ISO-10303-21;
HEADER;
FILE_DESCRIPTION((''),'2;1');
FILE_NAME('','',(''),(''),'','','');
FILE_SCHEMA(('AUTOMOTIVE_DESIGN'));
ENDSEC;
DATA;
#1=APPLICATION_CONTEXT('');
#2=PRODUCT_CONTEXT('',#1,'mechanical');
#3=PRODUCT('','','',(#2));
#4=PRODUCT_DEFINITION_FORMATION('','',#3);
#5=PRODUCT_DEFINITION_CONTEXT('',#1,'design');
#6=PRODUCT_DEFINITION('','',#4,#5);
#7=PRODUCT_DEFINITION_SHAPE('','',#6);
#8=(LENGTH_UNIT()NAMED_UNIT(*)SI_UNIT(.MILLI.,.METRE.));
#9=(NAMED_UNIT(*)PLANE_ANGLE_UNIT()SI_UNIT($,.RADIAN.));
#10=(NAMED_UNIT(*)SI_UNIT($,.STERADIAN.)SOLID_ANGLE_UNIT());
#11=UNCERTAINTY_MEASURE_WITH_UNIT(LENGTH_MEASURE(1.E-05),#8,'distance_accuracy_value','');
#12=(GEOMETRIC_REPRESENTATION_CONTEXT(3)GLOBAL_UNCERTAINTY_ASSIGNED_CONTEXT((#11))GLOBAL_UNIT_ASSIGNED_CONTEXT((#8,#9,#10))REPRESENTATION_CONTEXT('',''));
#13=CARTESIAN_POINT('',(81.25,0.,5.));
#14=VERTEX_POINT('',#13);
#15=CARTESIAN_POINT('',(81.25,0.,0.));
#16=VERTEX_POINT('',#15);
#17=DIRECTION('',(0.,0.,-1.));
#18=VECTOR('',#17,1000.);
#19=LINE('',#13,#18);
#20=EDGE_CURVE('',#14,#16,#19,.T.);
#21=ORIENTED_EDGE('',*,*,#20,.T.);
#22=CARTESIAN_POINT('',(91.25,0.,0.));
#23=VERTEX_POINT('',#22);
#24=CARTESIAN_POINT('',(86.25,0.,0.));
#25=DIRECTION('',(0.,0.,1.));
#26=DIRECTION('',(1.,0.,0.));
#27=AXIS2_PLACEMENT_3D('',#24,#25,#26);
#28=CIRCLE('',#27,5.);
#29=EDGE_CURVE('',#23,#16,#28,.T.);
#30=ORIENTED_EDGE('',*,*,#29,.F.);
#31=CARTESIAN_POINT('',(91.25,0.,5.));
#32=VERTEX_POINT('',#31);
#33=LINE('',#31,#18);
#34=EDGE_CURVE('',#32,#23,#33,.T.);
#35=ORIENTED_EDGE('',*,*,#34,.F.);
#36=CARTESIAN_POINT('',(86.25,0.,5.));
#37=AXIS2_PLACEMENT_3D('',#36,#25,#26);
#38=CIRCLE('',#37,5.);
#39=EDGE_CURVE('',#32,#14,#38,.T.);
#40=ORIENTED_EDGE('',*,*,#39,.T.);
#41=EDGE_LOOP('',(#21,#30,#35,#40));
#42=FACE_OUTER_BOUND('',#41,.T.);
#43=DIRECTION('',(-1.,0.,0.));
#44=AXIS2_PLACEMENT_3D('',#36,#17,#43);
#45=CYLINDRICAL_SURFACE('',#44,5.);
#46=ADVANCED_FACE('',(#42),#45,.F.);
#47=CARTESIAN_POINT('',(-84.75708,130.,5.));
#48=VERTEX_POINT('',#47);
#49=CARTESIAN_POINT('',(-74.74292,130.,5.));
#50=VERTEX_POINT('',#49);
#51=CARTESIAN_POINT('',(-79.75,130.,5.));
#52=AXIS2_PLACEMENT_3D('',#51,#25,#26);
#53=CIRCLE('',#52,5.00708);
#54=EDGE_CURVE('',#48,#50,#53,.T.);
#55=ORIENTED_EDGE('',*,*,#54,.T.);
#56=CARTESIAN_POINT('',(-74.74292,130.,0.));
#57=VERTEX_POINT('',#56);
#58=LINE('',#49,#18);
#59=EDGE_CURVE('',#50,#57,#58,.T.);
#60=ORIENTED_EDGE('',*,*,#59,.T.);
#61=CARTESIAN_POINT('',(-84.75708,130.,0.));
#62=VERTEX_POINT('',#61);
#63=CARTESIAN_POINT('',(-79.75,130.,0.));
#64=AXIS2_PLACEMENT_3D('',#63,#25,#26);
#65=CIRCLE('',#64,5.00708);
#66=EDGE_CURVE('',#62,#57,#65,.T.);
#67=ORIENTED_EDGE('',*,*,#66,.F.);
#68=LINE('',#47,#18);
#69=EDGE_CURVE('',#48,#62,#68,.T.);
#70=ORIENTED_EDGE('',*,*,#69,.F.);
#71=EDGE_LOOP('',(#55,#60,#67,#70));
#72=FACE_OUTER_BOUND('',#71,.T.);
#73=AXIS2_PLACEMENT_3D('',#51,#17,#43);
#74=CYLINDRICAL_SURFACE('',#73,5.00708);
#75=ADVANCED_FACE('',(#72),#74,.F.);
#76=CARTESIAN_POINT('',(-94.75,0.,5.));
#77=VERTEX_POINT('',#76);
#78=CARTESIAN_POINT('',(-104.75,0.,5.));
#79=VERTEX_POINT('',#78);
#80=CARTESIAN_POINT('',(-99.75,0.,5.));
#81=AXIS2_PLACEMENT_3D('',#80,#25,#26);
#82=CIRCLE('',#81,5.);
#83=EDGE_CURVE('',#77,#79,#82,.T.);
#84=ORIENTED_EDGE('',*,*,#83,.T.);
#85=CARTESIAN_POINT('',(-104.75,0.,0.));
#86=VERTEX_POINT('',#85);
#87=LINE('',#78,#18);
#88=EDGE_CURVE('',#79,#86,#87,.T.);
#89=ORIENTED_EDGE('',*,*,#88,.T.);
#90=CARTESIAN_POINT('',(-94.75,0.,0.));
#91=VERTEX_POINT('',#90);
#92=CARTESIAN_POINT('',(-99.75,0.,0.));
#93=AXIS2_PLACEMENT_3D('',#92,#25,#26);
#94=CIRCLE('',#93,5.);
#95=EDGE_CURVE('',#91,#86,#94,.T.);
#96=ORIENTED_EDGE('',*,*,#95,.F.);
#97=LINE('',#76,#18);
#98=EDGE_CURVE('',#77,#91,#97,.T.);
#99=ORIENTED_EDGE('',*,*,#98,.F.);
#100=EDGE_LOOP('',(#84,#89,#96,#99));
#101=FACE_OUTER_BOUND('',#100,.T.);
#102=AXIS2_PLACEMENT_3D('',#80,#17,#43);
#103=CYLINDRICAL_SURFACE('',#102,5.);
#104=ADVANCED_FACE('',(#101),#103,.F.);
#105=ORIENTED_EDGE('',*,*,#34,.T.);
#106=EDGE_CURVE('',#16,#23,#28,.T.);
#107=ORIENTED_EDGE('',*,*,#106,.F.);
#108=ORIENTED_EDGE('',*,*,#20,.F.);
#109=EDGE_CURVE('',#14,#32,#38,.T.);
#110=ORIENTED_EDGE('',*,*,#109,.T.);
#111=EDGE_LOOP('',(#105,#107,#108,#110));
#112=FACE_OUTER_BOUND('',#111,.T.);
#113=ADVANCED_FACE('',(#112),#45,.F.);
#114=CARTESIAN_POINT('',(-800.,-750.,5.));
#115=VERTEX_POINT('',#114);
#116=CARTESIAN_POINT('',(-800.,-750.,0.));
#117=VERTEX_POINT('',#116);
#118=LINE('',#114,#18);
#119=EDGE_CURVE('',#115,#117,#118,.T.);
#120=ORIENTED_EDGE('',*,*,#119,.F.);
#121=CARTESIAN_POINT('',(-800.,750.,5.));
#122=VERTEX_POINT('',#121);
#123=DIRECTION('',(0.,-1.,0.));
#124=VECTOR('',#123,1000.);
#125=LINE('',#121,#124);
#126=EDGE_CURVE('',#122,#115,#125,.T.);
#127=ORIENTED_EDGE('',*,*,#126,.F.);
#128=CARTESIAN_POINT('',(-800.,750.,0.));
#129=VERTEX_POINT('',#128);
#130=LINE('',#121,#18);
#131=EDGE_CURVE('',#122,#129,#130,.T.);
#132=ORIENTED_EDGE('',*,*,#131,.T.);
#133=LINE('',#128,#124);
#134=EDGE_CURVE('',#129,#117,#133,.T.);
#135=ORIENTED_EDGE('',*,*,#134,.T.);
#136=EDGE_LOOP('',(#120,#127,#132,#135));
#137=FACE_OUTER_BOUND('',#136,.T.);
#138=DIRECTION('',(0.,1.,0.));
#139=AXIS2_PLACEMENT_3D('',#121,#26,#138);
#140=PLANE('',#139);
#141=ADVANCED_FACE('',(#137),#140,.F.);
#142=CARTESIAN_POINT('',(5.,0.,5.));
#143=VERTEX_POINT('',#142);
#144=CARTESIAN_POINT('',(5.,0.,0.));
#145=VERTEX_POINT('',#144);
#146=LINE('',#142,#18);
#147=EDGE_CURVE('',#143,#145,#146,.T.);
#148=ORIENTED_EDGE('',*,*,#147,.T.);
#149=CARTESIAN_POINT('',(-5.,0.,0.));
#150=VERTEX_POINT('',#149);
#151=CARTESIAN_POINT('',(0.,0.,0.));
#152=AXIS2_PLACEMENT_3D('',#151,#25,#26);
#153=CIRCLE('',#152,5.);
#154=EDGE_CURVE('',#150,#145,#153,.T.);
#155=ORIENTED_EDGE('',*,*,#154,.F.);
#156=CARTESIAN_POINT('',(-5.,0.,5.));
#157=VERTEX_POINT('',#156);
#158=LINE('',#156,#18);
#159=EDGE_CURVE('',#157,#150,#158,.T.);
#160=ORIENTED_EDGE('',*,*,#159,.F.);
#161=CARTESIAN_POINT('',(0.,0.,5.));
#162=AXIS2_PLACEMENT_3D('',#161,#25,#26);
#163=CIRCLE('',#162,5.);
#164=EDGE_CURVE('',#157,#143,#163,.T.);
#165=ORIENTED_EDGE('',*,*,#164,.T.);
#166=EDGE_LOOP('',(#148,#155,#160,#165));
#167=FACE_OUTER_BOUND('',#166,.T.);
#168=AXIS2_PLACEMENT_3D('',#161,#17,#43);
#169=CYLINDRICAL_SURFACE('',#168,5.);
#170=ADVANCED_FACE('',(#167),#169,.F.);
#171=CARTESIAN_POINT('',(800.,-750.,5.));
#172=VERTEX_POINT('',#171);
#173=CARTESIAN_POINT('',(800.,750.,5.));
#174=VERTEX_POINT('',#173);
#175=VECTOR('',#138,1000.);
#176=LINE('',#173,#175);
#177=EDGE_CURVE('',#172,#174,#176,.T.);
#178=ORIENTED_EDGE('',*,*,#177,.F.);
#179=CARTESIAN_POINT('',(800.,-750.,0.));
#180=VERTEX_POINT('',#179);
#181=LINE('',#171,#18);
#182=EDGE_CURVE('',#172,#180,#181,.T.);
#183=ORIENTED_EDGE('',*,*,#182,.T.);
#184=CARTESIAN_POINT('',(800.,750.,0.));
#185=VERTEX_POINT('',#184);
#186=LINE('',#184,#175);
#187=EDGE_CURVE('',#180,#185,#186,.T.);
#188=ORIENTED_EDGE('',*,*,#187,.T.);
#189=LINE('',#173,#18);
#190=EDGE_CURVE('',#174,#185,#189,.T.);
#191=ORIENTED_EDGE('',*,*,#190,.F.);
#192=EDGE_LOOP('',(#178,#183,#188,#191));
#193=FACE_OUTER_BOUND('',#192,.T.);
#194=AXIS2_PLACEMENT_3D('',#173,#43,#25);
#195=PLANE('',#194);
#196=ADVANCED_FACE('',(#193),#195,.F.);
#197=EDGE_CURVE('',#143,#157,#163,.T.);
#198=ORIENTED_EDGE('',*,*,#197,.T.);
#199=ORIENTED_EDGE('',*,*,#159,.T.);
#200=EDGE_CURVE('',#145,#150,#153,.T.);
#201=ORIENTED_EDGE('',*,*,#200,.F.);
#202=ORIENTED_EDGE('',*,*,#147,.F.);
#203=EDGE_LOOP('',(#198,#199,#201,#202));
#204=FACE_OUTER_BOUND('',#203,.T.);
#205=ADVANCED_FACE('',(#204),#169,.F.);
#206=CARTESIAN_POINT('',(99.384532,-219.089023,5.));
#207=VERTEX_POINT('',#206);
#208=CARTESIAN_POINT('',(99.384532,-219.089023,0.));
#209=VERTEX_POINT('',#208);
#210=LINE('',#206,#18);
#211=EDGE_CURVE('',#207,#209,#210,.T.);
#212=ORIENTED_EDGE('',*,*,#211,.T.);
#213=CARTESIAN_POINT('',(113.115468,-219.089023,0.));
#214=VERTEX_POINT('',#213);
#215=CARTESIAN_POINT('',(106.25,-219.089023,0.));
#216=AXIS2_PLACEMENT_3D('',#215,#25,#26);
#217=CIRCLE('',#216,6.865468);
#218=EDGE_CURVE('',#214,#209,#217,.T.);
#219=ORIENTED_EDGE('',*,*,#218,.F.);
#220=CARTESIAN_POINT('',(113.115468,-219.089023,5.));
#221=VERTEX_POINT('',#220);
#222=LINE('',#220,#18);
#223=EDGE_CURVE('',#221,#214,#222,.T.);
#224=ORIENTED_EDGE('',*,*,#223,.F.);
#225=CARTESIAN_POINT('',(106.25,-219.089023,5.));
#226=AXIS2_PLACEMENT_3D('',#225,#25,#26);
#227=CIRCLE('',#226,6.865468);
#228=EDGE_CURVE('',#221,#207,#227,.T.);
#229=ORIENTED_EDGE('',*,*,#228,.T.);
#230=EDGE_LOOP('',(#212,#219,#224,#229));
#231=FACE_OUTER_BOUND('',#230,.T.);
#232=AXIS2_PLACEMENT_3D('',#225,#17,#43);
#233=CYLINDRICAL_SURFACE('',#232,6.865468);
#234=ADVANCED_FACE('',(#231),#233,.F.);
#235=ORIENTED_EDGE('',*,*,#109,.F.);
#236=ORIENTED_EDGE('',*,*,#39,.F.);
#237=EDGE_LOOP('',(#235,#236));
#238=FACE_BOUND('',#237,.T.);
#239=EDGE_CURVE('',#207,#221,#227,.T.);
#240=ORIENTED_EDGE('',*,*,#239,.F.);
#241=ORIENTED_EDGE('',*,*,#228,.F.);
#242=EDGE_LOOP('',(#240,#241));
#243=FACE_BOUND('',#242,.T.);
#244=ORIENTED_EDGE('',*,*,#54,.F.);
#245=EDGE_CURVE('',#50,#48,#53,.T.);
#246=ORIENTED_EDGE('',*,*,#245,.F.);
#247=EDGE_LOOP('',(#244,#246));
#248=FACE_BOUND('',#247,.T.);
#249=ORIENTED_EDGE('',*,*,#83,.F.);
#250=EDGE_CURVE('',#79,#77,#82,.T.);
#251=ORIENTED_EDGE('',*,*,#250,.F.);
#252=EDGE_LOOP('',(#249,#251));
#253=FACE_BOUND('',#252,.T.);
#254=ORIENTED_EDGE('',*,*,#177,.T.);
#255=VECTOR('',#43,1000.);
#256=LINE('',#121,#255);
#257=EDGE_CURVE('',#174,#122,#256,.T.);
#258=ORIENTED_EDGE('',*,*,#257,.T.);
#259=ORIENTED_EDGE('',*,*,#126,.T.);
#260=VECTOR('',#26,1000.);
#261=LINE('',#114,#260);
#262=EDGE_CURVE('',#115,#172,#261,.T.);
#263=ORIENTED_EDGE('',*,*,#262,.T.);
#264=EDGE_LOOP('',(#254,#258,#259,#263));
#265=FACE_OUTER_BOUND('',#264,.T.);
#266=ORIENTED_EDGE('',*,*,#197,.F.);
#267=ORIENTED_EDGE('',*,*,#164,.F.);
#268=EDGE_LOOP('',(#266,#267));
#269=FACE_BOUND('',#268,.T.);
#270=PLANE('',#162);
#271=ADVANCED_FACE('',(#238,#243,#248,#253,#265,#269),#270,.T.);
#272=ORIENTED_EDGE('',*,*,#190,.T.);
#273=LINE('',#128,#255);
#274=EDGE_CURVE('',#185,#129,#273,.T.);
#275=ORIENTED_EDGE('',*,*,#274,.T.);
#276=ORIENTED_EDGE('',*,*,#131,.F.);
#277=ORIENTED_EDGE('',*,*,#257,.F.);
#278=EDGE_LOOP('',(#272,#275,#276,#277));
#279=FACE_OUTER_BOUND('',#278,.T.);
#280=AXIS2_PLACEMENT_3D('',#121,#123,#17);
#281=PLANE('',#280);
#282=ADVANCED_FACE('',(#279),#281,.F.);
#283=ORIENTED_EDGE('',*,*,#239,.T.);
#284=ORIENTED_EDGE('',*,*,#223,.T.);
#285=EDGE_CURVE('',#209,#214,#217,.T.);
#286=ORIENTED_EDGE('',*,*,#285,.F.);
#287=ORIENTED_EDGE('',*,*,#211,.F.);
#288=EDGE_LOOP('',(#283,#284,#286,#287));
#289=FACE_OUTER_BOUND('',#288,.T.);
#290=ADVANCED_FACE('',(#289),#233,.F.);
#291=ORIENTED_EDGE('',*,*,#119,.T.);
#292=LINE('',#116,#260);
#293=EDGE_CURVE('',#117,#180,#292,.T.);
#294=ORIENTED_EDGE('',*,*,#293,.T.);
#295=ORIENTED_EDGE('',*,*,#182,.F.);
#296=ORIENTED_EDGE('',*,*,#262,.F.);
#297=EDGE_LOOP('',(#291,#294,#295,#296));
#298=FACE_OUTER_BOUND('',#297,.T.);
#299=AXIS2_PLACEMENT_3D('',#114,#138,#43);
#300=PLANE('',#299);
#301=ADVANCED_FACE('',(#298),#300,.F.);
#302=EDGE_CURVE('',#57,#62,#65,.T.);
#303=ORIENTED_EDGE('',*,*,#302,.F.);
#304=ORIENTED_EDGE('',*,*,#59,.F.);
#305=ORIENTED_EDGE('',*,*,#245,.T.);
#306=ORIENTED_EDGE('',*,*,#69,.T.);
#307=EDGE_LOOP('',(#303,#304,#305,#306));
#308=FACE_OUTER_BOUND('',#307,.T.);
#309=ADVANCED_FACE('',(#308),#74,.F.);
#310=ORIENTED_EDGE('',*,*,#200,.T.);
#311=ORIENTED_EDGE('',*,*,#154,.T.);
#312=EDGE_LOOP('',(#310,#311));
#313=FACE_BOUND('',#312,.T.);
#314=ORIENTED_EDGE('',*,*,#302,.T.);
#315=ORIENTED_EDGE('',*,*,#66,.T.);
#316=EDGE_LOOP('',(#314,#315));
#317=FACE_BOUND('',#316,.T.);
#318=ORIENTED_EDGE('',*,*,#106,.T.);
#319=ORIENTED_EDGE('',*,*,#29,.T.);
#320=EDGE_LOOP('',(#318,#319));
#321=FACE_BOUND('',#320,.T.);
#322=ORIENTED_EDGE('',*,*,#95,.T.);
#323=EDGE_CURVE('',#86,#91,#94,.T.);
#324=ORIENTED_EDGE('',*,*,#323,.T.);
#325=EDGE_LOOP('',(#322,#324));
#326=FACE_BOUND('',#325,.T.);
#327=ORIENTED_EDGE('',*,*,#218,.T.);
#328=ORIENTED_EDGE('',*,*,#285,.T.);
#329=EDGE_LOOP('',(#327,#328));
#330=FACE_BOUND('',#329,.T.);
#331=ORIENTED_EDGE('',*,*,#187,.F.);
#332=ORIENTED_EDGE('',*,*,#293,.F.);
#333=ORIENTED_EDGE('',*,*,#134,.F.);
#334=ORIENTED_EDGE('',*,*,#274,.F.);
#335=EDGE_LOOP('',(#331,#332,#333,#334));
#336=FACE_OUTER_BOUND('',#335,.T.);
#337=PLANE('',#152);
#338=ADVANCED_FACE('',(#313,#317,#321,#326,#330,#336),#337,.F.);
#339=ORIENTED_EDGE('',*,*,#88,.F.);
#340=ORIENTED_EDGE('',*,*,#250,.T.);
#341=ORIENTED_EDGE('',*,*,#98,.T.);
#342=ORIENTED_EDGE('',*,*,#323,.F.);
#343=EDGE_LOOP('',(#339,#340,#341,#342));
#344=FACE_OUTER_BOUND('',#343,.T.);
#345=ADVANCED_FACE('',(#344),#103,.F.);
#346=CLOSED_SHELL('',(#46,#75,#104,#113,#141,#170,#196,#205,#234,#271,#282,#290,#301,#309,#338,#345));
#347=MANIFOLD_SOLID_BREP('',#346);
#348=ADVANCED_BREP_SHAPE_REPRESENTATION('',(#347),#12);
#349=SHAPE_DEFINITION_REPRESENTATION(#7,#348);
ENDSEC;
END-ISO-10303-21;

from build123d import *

# Parameters (mm, degrees)
SKETCH1_W           = 1600
SKETCH1_H           = 1500
SKETCH1_R           = 5
SKETCH1_R_2         = 6.865468099
SKETCH1_R_3         = 5.007080458
BOSS_EXTRUDE1_DEPTH = 5


with BuildPart() as part:
    # Sketch1 → Boss-Extrude1 (new body)
    with BuildSketch(Plane.XY):
        Rectangle(SKETCH1_W, SKETCH1_H)
        Circle(SKETCH1_R, mode=Mode.SUBTRACT)
        with Locations((-99.75, 0)):
            Circle(SKETCH1_R, mode=Mode.SUBTRACT)
        with Locations((86.25, 0)):
            Circle(SKETCH1_R, mode=Mode.SUBTRACT)
        with Locations((106.25, -219.089023002)):
            Circle(SKETCH1_R_2, mode=Mode.SUBTRACT)
        with Locations((-79.75, 130)):
            Circle(SKETCH1_R_3, mode=Mode.SUBTRACT)
    extrude(amount=BOSS_EXTRUDE1_DEPTH)


solid = part.part
